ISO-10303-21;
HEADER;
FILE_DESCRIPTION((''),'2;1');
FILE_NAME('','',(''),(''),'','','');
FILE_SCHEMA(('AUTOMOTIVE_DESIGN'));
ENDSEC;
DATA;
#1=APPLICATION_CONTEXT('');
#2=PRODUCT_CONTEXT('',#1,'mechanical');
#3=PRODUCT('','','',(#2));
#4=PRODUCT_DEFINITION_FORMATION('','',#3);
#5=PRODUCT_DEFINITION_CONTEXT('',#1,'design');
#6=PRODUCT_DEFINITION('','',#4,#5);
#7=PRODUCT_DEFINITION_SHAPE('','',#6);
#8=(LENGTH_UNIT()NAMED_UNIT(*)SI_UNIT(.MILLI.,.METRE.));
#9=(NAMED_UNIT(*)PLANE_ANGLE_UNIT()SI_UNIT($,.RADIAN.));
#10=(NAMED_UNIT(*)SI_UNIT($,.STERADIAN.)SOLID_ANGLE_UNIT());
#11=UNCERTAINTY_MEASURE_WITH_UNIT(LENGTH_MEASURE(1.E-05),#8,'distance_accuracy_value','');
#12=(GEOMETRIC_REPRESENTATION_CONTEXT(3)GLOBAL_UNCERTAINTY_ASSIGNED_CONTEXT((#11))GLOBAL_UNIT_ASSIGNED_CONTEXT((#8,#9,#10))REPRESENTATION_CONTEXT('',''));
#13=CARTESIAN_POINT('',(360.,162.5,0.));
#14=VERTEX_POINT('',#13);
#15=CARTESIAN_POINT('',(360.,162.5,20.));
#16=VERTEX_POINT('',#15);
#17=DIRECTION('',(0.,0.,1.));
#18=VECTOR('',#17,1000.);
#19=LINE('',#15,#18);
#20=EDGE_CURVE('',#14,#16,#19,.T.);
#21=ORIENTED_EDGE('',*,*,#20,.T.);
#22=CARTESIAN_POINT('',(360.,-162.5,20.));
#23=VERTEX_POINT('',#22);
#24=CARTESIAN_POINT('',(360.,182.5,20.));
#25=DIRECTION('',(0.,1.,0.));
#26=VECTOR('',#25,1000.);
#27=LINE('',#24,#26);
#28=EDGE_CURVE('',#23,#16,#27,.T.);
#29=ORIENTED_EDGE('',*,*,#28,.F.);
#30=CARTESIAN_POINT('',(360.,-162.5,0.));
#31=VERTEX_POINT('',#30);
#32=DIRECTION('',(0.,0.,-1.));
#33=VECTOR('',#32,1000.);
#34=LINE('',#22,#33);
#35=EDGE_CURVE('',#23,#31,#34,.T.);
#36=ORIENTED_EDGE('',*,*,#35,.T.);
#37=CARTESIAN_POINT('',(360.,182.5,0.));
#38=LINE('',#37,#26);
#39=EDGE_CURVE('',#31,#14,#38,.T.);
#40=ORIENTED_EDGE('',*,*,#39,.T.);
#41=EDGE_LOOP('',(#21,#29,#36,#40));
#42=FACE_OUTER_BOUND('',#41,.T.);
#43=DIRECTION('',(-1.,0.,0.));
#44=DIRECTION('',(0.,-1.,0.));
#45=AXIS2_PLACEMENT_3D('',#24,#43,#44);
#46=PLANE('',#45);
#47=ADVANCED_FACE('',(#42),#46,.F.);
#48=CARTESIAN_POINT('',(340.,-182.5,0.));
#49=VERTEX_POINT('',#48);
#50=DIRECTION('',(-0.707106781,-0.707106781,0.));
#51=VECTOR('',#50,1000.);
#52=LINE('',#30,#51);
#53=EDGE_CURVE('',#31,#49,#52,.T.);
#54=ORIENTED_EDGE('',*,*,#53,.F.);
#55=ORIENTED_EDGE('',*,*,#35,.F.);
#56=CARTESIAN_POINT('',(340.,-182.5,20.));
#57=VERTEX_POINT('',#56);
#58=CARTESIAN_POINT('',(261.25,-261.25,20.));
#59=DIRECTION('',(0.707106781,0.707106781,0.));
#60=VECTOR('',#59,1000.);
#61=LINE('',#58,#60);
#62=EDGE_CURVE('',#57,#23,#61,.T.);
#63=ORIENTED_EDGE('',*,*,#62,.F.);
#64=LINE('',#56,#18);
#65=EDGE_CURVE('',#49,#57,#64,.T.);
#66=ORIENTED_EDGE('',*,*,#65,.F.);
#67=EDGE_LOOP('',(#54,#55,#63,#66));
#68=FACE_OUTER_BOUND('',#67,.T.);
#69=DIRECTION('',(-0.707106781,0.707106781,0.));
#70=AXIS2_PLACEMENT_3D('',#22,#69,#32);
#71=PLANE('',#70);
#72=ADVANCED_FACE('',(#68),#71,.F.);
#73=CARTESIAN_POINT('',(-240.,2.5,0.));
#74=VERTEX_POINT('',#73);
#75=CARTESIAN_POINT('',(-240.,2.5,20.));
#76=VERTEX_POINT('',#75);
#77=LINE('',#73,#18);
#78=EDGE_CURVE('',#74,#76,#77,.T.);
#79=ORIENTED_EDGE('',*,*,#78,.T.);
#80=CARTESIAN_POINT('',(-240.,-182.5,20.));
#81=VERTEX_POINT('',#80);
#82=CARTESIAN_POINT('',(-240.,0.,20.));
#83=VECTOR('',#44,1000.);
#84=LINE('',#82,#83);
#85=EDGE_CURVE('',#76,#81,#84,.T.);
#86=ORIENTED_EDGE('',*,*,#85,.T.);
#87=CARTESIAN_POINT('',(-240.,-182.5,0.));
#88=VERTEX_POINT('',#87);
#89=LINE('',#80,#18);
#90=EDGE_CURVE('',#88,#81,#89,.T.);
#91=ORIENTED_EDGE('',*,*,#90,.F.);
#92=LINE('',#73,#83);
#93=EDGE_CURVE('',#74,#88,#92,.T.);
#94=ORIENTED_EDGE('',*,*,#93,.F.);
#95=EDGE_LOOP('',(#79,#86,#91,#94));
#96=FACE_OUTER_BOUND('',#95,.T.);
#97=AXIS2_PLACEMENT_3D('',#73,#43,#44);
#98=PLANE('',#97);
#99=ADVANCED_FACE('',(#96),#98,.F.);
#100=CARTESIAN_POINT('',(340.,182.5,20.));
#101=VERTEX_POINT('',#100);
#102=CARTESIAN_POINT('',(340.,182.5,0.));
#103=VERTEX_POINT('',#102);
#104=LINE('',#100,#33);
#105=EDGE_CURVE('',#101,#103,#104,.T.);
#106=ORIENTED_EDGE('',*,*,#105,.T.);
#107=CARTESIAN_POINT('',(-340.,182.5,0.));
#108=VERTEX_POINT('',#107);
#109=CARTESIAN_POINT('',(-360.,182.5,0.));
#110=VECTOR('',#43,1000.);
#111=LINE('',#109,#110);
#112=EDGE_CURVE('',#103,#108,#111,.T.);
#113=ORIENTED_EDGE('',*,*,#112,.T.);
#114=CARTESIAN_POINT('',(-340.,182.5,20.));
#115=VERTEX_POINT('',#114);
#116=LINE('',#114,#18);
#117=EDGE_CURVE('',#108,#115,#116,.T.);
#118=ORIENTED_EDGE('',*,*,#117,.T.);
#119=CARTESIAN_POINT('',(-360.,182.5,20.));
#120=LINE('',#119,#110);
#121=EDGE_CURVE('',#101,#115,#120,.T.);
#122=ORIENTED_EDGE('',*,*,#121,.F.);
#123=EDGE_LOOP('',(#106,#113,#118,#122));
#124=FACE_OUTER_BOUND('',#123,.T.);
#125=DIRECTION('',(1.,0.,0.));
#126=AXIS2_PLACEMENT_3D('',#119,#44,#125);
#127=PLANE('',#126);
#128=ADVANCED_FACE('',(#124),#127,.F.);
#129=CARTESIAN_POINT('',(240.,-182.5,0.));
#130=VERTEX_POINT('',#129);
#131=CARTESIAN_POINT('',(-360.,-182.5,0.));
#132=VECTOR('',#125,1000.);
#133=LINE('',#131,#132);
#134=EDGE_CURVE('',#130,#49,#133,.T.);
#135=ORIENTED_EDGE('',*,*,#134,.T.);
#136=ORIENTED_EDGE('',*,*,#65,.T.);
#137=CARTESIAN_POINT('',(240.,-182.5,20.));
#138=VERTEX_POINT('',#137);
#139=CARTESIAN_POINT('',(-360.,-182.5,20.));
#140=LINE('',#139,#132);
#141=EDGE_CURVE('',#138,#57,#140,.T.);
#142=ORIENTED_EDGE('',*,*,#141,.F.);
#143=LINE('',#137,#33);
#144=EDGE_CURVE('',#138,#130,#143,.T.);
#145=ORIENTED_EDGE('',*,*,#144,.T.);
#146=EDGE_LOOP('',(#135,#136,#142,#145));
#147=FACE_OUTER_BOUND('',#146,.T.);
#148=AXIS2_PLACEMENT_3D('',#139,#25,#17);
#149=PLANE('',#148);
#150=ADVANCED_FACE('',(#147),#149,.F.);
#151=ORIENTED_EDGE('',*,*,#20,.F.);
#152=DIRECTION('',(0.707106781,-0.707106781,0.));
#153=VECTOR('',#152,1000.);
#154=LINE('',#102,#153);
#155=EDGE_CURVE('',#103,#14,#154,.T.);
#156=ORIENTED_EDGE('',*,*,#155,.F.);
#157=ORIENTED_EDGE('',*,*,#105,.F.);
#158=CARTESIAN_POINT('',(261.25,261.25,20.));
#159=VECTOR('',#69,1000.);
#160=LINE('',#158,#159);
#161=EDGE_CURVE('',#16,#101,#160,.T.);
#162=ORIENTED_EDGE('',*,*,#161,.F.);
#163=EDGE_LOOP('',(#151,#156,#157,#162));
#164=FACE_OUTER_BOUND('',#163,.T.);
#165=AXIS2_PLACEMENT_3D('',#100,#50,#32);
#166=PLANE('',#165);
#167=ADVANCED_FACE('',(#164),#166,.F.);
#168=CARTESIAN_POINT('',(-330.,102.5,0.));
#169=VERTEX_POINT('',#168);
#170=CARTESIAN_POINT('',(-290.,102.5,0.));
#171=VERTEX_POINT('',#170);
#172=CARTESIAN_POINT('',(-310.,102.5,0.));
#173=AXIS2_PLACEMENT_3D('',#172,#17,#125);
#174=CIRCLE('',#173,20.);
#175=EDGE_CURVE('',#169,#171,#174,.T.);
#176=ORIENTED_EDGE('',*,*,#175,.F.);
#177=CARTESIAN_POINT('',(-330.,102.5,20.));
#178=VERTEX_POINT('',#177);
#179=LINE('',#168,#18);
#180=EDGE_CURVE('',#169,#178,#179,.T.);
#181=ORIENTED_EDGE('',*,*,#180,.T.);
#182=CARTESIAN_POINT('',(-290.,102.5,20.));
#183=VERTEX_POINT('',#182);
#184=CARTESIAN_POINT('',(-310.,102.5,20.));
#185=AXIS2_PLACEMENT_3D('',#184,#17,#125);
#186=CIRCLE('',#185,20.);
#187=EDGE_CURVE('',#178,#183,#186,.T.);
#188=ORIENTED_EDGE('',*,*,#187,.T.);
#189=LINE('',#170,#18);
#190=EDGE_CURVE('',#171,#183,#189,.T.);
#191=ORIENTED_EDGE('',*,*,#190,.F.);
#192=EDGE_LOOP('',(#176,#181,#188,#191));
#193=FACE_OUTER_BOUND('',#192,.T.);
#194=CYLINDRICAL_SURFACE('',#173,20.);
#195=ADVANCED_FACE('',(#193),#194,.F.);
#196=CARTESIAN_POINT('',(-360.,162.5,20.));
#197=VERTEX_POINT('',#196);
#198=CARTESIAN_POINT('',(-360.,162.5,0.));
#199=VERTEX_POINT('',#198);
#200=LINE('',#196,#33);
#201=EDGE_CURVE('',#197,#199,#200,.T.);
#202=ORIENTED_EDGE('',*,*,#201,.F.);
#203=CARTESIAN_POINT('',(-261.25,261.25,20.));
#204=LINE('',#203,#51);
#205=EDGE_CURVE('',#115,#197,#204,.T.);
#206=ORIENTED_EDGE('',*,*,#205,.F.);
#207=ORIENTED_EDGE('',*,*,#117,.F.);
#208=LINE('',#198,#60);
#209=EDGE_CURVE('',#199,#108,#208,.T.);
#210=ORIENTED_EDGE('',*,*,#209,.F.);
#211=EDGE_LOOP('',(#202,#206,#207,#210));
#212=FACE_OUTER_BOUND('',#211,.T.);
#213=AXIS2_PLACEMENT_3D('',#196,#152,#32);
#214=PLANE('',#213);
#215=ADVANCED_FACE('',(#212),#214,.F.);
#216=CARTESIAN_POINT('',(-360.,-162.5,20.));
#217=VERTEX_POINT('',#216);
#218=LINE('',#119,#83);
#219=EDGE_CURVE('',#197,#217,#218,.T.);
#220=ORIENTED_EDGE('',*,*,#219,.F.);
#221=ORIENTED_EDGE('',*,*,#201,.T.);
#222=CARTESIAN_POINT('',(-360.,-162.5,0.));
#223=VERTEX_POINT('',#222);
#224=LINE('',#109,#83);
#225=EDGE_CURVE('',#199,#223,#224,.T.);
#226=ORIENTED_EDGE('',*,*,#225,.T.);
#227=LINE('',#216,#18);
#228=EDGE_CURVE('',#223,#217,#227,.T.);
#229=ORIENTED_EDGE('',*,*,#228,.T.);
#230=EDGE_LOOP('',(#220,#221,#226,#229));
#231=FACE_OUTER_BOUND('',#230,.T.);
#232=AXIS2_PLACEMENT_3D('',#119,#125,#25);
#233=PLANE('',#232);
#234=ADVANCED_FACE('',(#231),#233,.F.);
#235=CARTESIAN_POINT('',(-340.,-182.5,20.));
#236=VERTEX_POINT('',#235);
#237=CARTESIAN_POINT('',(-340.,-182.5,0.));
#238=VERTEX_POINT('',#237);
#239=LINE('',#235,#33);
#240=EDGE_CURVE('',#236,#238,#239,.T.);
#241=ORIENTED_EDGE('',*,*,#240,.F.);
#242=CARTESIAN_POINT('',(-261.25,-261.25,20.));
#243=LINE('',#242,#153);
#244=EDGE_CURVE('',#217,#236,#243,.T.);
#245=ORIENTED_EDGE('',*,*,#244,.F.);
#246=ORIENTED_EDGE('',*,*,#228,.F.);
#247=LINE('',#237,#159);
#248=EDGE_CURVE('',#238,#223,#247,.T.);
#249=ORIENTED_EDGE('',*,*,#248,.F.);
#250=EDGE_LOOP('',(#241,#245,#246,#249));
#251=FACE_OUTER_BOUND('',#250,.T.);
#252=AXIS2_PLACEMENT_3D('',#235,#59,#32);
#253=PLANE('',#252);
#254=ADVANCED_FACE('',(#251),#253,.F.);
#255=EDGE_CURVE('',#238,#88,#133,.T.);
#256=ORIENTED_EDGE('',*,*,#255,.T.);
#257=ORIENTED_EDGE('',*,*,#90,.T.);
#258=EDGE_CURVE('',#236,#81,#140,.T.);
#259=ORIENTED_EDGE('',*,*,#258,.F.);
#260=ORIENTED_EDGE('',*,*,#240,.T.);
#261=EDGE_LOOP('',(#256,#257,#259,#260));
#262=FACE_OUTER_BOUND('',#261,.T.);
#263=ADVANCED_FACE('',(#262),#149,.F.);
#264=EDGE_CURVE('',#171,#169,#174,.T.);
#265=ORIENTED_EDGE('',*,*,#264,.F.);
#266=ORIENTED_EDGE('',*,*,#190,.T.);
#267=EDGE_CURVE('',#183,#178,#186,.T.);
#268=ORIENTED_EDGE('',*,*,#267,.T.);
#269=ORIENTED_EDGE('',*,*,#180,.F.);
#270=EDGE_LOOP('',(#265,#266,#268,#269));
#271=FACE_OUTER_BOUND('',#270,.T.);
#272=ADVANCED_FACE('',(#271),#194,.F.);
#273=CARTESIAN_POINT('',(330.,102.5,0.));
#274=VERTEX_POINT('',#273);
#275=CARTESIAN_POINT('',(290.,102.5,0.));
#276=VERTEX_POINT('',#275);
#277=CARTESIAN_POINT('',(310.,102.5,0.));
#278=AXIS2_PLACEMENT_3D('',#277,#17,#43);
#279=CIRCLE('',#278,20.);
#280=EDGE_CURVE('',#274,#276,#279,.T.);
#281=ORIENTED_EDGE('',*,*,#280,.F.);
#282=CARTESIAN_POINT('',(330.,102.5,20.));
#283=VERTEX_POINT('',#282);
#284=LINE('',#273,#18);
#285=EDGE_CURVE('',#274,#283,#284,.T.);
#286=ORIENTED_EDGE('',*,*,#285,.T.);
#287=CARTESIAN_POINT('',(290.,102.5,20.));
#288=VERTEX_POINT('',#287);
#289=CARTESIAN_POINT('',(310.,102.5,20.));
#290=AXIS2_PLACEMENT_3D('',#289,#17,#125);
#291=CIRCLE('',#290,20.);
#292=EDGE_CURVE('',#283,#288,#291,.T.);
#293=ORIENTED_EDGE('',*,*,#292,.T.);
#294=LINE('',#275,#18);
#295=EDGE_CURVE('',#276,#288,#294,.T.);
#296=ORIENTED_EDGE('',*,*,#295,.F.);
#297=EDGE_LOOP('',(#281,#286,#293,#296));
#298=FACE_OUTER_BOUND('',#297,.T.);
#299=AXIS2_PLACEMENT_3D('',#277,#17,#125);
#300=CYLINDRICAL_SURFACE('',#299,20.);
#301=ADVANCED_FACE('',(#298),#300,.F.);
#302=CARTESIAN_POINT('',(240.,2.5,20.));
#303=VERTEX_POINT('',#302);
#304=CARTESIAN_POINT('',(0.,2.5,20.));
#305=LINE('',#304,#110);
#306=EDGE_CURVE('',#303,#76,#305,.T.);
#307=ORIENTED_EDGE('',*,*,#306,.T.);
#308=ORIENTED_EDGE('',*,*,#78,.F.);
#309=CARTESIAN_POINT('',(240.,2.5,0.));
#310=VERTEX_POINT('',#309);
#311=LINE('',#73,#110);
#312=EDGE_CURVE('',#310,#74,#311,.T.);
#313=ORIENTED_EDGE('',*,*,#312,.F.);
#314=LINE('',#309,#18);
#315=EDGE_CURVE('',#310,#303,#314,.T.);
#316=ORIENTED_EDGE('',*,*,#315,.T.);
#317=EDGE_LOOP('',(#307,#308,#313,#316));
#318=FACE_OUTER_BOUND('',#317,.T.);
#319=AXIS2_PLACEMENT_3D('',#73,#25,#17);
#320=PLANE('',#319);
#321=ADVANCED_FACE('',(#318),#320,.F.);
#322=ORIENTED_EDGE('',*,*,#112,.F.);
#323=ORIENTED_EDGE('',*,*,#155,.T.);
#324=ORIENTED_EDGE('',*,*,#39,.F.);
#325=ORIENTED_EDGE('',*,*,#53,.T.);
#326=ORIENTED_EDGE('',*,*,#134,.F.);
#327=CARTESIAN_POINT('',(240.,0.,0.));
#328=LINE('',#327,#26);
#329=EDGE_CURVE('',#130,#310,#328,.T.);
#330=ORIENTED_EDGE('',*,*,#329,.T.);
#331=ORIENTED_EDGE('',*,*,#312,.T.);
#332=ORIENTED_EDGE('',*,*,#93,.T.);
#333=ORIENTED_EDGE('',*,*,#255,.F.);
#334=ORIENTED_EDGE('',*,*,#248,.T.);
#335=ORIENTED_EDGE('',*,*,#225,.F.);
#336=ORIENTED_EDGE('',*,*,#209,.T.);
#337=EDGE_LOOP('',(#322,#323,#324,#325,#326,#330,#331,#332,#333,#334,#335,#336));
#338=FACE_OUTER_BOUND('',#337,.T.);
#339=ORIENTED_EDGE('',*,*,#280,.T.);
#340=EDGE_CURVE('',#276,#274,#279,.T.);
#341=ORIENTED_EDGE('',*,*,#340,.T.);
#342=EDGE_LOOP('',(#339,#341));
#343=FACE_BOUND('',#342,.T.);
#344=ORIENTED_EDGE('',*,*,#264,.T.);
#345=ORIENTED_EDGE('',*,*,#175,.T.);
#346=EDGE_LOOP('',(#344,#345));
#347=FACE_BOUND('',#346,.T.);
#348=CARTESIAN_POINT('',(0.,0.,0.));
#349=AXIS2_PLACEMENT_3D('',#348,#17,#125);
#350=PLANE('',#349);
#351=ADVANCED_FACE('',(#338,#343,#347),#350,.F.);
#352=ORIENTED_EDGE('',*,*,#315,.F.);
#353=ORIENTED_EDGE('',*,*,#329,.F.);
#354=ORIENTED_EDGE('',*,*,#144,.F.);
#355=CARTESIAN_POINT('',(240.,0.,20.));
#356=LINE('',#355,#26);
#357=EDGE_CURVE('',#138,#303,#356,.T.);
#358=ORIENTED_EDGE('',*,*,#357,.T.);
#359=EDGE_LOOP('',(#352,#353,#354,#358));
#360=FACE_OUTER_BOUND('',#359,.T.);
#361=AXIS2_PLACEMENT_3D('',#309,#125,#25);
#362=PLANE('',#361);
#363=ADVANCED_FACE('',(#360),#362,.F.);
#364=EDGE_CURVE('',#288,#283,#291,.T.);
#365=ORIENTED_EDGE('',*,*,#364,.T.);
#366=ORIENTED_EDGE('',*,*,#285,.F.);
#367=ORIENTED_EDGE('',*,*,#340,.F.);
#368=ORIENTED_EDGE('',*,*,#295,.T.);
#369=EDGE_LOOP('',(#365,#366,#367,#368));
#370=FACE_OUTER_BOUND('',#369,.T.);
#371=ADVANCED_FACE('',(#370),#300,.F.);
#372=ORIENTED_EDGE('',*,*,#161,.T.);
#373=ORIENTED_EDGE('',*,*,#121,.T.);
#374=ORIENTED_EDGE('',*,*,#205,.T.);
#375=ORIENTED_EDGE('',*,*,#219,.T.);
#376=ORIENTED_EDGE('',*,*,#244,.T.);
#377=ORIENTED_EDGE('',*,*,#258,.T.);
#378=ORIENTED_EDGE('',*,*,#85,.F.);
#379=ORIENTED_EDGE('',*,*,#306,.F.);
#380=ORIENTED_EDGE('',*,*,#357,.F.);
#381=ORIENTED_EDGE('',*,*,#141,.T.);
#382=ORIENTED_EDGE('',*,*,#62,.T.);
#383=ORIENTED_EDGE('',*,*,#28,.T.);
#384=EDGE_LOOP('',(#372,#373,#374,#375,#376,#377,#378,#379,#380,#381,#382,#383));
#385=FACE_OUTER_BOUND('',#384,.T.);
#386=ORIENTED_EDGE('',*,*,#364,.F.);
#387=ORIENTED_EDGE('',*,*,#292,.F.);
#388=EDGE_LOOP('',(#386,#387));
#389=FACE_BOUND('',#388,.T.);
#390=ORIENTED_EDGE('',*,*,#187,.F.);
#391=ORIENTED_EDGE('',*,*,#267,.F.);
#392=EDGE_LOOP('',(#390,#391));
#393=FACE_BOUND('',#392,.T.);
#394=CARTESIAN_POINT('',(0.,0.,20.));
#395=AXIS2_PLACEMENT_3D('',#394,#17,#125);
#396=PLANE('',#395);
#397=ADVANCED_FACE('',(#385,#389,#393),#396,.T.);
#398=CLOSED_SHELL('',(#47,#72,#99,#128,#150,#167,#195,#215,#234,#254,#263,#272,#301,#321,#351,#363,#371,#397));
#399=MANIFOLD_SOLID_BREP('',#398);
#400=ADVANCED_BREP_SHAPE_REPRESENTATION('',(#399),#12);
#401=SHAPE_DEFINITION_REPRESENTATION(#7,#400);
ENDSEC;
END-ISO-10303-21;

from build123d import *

# Parameters (mm, degrees)
SKETCH1_W               = 720
SKETCH1_H               = 365
BOSS_EXTRUDE1_DEPTH     = 20
CUT_EXTRUDE1_DEPTH      = 405.111680108
CUT_EXTRUDE1_DEPTH_BACK = 405.111680108
SKETCH2_R               = 20
CHAMFER1_SIZE           = 20
CHAMFER2_SIZE           = 20
CUT_EXTRUDE2_DEPTH      = 405.111680108
CUT_EXTRUDE2_DEPTH_BACK = 405.111680108
SKETCH4_W               = 480
SKETCH4_H               = 370


with BuildPart() as part:
    # Sketch1 → Boss-Extrude1 (new body)
    with BuildSketch(Plane.XY):
        Rectangle(SKETCH1_W, SKETCH1_H)
    extrude(amount=BOSS_EXTRUDE1_DEPTH)

    # Sketch2 → Cut-Extrude1 (cut, two sides: drawn at the far end of the back side and taken through both)
    with BuildSketch(Plane.XY.offset(20).offset(-CUT_EXTRUDE1_DEPTH_BACK)):
        with Locations((-310, 102.5)):
            Circle(SKETCH2_R)
        with Locations((310, 102.5)):
            Circle(SKETCH2_R)
    extrude(amount=CUT_EXTRUDE1_DEPTH + CUT_EXTRUDE1_DEPTH_BACK, mode=Mode.SUBTRACT)

    # Chamfer1
    chamfer1_edges = [part.edges().sort_by_distance(p)[0] for p in [
        (-360, 182.5, 10),
        (360, 182.5, 10),
    ]]
    chamfer(chamfer1_edges, length=CHAMFER1_SIZE)

    # Chamfer2
    chamfer2_edges = [part.edges().sort_by_distance(p)[0] for p in [
        (360, -182.5, 10),
        (-360, -182.5, 10),
    ]]
    chamfer(chamfer2_edges, length=CHAMFER2_SIZE)

    # Sketch4 → Cut-Extrude2 (cut, two sides: drawn at the far end of the back side and taken through both)
    with BuildSketch(Plane.XY.offset(20).offset(-CUT_EXTRUDE2_DEPTH_BACK)):
        with Locations((0, -182.5)):
            Rectangle(SKETCH4_W, SKETCH4_H)
    extrude(amount=CUT_EXTRUDE2_DEPTH + CUT_EXTRUDE2_DEPTH_BACK, mode=Mode.SUBTRACT)


solid = part.part
